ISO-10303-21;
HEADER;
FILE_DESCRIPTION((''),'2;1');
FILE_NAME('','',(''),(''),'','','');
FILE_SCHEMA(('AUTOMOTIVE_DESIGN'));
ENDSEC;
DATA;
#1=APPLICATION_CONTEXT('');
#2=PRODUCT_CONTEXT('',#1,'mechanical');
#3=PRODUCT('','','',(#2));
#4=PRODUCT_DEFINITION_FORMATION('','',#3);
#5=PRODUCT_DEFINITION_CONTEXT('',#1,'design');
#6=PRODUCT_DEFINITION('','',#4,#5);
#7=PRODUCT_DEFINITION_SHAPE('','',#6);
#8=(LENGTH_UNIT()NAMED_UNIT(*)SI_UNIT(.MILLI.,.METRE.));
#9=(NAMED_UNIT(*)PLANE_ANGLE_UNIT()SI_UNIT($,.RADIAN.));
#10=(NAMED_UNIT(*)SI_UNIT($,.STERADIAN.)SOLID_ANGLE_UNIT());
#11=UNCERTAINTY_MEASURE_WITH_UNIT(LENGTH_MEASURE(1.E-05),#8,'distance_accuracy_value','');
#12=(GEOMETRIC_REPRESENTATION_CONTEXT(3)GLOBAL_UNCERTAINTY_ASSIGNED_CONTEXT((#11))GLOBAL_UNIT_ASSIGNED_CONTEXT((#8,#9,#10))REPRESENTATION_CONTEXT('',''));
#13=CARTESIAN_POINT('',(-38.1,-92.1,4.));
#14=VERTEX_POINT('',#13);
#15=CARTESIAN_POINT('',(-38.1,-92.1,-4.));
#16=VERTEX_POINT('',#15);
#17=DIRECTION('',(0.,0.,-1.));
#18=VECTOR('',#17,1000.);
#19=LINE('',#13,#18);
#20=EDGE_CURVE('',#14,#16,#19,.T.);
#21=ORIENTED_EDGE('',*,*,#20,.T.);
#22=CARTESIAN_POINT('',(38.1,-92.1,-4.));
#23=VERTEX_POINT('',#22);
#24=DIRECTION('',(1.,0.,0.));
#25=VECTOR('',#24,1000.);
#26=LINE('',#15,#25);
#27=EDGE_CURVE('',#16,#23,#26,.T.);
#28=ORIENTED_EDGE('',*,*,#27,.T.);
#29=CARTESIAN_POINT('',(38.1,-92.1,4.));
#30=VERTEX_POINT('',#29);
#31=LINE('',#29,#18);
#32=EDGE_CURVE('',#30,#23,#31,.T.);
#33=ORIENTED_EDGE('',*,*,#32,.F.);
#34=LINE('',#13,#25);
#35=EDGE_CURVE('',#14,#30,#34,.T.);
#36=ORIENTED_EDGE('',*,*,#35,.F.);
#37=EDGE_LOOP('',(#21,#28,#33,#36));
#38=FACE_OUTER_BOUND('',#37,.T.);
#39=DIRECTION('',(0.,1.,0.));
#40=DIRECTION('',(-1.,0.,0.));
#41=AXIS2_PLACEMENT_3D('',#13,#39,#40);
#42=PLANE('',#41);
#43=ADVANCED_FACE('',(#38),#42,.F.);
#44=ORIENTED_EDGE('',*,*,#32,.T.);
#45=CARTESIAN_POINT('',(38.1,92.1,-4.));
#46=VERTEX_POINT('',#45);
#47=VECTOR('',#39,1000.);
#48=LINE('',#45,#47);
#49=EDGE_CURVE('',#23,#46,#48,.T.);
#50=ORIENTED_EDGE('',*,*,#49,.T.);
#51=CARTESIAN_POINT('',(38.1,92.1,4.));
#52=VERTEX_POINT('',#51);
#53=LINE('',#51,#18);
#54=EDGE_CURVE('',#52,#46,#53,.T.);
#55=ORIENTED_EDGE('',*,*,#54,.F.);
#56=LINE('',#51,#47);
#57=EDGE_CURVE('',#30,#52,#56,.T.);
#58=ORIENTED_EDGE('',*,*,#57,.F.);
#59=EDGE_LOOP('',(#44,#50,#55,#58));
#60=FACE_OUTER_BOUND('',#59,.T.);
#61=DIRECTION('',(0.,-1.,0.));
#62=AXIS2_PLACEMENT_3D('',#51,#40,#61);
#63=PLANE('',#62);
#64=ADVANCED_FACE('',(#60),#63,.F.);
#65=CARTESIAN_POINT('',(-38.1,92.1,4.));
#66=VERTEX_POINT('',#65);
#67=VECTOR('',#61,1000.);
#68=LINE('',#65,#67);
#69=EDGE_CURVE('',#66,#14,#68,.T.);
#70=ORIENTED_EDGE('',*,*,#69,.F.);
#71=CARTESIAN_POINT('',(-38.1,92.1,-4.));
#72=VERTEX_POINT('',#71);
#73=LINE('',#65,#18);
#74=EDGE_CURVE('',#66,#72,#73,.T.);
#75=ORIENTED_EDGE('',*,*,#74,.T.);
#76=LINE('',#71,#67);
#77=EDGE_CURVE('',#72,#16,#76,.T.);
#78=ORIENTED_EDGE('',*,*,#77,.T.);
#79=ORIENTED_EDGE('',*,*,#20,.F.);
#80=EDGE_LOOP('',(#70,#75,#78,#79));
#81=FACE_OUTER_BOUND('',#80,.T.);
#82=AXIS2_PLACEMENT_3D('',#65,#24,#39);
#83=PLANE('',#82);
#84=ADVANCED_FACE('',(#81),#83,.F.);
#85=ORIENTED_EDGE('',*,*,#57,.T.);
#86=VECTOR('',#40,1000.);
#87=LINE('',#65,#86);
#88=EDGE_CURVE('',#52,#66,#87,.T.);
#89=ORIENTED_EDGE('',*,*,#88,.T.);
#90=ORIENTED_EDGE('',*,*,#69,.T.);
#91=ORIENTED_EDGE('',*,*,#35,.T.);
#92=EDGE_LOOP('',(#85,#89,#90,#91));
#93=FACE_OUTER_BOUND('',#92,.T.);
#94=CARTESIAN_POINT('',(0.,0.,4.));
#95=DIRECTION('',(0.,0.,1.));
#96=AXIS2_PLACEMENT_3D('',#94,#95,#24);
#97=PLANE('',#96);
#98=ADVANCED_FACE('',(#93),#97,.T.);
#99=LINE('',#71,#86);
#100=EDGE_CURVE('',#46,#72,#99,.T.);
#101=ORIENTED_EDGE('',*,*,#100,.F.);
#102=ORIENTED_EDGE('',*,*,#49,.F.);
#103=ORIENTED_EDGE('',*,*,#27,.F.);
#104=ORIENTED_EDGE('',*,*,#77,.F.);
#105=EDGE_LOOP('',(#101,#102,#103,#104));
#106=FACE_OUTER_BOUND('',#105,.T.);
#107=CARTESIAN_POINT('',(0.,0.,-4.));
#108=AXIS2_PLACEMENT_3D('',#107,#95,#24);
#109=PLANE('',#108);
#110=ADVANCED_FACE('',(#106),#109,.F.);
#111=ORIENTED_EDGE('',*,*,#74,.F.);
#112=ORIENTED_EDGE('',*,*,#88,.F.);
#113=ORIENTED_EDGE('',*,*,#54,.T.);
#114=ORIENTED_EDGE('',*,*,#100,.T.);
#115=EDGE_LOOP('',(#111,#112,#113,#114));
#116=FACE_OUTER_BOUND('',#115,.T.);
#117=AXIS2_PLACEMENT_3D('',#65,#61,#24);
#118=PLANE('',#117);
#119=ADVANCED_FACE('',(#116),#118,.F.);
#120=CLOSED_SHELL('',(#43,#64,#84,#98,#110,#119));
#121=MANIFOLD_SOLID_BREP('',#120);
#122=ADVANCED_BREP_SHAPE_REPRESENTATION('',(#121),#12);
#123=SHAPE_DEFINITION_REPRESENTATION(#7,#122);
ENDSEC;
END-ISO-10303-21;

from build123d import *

# Parameters (mm, degrees)
SKETCH1_W           = 76.2
SKETCH1_H           = 184.2
BOSS_EXTRUDE1_DEPTH = 4


with BuildPart() as part:
    # Sketch1 → Boss-Extrude1 (new, symmetric)
    with BuildSketch(Plane.XY):
        Rectangle(SKETCH1_W, SKETCH1_H)
    extrude(amount=BOSS_EXTRUDE1_DEPTH, both=True)


solid = part.part
